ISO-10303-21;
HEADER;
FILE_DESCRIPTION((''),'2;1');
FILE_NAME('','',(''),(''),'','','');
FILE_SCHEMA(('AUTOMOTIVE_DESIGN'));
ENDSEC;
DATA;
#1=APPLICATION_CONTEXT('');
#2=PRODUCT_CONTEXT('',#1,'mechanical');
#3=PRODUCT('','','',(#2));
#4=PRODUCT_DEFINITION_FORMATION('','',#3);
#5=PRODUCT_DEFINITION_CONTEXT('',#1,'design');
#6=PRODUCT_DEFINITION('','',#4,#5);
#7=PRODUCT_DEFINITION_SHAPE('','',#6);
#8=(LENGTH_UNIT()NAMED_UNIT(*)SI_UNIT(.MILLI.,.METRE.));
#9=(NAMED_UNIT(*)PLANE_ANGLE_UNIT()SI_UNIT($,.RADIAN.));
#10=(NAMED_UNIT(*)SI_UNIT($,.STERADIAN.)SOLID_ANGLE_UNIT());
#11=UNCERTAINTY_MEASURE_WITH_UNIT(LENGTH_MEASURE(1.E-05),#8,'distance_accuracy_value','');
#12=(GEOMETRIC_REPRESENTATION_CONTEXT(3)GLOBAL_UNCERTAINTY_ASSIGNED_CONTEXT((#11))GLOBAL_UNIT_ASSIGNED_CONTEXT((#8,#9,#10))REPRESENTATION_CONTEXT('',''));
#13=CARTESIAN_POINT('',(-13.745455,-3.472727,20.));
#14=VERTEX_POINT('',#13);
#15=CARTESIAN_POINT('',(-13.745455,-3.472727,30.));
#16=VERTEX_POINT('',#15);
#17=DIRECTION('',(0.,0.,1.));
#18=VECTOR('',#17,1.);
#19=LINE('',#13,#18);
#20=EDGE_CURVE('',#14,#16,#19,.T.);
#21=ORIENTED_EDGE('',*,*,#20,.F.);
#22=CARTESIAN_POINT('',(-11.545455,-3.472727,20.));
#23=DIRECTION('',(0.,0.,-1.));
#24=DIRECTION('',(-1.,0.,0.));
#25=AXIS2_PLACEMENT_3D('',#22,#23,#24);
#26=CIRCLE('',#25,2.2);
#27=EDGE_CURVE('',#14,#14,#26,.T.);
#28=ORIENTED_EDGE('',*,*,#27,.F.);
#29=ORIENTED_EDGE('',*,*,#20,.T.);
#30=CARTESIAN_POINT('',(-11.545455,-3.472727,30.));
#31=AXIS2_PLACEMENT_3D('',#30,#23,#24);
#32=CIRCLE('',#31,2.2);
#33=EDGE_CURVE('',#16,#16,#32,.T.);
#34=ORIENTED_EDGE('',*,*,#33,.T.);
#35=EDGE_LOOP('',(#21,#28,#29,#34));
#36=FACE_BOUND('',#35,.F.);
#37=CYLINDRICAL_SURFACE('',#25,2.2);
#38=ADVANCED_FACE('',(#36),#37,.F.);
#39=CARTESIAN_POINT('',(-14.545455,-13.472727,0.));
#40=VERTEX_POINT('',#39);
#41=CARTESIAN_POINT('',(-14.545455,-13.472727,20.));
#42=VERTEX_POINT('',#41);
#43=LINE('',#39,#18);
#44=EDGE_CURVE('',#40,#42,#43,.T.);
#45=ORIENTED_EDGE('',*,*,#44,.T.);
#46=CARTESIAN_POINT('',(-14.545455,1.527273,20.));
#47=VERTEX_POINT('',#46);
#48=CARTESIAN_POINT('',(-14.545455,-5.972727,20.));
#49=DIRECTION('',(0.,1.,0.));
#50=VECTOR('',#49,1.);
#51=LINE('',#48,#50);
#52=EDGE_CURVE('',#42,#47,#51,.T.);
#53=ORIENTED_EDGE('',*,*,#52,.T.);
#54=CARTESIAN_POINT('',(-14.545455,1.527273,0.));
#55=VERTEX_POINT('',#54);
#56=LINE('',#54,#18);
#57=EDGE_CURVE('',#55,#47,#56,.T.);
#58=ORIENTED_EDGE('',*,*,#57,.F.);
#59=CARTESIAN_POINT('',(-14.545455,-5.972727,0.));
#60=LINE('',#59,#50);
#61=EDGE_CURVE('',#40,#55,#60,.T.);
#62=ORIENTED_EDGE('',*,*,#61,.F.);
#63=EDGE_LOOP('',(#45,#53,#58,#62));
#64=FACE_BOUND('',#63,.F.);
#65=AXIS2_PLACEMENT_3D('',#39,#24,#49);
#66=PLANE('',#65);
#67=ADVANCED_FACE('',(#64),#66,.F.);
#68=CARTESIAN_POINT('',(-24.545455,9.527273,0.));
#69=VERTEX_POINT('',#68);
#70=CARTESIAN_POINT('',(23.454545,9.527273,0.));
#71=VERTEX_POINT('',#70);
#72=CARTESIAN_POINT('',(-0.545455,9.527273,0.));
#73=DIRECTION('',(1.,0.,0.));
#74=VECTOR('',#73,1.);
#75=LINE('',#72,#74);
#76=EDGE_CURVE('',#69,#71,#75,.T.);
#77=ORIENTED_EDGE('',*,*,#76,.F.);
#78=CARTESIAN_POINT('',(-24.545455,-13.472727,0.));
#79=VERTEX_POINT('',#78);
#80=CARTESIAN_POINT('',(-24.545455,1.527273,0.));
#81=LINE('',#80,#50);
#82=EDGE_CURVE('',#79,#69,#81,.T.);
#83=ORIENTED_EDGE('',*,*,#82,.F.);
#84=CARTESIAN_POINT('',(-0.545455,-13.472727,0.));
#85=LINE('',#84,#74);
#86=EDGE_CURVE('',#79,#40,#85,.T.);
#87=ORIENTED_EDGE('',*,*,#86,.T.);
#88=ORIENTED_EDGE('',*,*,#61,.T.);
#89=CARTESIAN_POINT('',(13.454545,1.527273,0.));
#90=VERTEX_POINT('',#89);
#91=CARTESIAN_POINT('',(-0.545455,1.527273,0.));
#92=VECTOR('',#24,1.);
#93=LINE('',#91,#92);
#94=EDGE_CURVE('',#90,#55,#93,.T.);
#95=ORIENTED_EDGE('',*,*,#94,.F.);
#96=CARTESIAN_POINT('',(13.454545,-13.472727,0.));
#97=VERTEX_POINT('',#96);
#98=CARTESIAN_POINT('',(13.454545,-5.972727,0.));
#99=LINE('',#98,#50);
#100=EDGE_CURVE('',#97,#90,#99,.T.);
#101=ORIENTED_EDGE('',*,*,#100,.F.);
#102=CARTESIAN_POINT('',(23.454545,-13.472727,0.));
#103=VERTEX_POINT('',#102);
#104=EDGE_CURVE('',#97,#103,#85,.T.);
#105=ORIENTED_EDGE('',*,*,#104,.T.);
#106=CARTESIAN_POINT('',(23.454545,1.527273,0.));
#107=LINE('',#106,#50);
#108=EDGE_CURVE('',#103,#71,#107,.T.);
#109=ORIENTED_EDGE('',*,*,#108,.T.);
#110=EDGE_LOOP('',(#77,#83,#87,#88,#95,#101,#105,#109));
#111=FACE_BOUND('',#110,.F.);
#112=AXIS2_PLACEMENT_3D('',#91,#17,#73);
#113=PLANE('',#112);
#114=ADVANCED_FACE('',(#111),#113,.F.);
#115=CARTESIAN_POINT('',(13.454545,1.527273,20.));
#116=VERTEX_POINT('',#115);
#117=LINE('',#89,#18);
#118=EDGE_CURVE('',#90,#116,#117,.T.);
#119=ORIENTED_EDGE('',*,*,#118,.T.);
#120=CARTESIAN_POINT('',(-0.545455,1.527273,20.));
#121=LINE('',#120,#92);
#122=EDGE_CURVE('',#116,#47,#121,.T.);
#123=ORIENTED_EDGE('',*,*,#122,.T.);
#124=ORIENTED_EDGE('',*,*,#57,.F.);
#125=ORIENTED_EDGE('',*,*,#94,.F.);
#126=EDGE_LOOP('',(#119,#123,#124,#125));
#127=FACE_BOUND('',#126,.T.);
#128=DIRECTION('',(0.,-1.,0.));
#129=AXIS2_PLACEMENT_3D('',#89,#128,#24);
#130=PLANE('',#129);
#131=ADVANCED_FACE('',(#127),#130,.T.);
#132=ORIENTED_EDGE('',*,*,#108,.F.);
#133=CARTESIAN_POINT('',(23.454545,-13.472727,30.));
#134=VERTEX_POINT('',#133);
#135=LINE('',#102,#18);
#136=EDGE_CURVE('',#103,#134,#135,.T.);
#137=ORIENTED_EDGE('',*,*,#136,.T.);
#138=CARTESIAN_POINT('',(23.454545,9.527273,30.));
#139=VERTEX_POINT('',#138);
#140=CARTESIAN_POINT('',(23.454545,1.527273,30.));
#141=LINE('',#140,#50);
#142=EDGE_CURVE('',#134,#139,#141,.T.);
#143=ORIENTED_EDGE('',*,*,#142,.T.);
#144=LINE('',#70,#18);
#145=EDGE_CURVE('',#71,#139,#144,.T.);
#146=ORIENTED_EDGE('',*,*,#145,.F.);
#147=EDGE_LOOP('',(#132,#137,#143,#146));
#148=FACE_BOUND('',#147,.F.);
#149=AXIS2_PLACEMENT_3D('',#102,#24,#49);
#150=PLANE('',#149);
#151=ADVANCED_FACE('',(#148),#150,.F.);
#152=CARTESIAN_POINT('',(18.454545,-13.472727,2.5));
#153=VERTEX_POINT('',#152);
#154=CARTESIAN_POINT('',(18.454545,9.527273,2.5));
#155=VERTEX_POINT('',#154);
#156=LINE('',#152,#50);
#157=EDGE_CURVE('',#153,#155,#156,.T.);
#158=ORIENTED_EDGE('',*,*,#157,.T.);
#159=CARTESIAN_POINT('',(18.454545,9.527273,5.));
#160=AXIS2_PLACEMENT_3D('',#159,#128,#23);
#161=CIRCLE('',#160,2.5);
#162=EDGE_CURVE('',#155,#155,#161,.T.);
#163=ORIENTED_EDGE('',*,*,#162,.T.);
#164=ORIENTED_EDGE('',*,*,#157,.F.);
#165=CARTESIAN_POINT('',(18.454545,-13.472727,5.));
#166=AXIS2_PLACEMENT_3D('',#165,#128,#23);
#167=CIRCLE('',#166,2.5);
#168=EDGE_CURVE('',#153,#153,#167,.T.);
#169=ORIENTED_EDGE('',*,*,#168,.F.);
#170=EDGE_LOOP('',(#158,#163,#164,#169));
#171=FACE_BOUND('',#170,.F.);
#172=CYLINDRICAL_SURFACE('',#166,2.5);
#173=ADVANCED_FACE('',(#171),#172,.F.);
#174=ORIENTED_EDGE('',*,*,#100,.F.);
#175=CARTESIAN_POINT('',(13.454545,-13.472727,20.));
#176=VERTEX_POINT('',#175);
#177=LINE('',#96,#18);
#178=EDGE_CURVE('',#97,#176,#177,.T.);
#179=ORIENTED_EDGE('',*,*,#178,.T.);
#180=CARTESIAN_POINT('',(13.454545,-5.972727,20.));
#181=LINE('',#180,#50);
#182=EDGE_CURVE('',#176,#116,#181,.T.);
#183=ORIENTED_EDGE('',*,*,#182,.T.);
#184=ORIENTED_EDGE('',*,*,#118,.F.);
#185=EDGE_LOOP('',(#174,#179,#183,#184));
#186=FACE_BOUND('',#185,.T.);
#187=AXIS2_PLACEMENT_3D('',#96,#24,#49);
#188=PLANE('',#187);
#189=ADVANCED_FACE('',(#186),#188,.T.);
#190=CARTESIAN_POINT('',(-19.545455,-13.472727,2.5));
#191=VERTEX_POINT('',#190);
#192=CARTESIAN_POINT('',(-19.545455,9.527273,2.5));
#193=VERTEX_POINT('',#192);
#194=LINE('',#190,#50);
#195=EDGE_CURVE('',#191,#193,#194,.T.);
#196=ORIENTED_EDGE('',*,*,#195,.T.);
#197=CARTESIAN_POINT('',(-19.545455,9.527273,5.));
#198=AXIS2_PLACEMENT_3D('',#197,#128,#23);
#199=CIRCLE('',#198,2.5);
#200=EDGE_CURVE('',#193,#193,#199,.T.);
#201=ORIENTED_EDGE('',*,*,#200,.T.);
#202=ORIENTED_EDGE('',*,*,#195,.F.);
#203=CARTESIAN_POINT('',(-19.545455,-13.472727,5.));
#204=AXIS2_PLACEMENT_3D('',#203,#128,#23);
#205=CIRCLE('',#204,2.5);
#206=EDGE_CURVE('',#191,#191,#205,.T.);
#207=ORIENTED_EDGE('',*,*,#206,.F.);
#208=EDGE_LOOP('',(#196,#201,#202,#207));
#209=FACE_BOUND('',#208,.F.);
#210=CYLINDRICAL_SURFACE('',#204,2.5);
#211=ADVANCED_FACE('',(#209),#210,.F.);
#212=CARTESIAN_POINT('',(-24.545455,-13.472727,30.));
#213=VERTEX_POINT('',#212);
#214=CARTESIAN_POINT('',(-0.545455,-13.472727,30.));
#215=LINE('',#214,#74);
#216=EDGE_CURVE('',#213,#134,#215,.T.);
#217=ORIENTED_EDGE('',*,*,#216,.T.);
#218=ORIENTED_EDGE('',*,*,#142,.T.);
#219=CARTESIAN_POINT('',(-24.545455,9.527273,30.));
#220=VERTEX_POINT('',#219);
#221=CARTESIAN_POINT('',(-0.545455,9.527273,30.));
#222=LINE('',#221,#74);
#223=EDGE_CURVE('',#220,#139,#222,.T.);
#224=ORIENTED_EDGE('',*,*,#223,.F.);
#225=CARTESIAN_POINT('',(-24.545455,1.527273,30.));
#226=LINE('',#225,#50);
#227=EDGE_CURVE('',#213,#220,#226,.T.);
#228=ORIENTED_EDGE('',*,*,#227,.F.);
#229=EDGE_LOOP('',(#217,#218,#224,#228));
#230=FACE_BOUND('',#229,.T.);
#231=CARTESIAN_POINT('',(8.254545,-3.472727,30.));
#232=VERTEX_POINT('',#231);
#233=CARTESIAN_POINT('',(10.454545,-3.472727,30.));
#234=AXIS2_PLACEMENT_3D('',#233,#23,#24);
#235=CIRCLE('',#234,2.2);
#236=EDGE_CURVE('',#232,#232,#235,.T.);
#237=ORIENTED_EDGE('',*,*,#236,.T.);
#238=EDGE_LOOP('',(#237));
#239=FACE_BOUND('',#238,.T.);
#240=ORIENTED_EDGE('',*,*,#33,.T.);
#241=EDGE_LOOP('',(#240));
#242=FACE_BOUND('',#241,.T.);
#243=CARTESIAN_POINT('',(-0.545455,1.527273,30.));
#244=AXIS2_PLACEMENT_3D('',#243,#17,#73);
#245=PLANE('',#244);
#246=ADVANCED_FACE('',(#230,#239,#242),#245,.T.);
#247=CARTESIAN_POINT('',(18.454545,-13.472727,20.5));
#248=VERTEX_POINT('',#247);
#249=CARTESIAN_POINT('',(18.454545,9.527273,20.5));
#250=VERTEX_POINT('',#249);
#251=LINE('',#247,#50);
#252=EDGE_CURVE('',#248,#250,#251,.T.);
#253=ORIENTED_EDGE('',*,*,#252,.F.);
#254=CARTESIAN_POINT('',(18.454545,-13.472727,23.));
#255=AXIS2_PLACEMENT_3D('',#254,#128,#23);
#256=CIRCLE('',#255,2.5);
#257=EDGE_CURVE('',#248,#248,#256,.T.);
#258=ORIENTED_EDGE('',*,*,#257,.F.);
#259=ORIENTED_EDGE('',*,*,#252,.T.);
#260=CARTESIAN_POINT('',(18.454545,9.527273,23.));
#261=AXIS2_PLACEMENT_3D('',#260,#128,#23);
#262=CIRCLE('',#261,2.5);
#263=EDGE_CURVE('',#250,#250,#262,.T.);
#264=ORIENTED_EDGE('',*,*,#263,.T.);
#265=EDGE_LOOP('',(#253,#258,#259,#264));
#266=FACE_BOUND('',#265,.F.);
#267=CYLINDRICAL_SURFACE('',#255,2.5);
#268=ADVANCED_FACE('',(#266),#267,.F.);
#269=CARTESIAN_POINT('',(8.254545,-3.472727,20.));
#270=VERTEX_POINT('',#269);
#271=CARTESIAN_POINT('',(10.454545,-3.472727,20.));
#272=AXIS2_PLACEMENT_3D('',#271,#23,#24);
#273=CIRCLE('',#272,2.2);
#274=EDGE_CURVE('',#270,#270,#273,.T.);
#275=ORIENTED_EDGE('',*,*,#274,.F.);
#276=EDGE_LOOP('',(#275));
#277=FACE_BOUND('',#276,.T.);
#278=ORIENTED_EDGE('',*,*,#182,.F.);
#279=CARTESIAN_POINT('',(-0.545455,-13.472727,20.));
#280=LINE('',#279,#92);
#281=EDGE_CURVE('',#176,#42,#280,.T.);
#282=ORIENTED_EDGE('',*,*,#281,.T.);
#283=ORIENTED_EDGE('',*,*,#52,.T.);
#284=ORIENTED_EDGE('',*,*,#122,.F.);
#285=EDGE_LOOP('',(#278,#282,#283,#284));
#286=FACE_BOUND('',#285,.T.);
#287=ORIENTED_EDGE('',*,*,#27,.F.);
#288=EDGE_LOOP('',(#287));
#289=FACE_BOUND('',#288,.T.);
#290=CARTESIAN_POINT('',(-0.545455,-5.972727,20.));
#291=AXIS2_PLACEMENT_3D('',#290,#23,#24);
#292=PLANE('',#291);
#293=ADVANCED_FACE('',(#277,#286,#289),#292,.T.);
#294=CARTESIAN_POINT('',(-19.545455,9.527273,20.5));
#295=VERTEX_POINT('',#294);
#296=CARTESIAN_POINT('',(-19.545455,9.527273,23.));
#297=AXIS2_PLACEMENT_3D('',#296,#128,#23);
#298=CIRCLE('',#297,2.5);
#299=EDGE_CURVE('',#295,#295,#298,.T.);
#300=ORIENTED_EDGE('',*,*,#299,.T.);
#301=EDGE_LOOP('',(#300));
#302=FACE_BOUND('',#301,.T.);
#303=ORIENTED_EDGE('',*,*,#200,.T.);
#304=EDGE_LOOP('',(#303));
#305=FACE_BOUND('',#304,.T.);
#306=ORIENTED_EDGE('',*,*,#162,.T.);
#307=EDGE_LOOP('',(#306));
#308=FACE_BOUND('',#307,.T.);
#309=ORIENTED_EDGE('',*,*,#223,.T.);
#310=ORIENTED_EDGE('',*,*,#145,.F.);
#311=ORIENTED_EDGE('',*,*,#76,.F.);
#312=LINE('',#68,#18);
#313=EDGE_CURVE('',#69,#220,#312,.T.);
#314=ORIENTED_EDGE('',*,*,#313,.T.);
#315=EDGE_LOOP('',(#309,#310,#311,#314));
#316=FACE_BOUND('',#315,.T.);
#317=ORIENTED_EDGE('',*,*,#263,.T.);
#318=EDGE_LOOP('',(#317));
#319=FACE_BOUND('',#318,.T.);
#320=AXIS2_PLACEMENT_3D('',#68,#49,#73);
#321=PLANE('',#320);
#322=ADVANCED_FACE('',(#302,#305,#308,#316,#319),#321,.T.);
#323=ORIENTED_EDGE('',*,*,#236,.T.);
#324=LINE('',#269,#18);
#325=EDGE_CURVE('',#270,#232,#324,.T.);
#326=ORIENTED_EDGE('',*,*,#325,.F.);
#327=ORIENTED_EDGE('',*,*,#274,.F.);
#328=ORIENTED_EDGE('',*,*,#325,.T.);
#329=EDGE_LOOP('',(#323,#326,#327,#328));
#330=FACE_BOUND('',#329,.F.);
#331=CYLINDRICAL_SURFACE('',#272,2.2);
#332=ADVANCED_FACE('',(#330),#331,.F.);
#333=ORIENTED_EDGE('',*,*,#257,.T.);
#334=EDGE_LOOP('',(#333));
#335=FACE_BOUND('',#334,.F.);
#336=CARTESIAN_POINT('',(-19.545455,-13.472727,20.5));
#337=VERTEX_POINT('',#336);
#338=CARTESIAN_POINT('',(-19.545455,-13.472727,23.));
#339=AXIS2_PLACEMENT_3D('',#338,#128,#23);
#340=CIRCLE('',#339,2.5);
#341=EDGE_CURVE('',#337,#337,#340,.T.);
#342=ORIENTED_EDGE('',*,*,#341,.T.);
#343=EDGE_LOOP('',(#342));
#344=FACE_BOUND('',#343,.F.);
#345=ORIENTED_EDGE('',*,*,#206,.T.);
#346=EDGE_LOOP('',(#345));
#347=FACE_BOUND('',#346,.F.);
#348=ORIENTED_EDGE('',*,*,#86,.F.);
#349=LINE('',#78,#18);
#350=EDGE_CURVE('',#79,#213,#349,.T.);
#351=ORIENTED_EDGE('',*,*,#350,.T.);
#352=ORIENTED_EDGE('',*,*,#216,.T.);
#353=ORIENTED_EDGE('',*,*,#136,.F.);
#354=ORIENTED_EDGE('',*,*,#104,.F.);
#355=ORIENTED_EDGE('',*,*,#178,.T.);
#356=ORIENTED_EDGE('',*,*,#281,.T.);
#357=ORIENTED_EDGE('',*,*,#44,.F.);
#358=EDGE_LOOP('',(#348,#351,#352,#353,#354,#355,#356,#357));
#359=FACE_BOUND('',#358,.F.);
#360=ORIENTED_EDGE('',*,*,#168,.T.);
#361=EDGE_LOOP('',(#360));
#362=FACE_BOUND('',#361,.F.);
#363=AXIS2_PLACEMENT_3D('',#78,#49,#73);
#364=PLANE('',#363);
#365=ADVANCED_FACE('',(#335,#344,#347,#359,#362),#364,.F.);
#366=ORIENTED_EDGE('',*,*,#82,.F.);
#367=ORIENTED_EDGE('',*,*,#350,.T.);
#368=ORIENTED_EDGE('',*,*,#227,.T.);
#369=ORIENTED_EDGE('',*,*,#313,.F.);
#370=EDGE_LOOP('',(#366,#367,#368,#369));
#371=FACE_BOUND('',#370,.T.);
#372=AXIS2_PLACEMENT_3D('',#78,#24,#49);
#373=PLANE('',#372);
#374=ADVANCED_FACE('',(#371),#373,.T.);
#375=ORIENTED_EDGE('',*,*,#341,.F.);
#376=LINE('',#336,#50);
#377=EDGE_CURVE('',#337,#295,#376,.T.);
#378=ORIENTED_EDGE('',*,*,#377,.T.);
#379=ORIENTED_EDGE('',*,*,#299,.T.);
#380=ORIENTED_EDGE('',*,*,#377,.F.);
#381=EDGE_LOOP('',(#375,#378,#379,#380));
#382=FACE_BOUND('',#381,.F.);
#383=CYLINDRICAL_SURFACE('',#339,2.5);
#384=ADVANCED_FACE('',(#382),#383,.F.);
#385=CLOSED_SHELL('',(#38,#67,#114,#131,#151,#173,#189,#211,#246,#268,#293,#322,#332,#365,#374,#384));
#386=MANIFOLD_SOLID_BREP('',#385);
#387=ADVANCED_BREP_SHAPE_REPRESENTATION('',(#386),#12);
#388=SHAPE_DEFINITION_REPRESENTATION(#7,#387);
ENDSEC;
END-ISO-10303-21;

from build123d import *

# Parameters (mm, degrees)
SKETCH_1_W          = 48
SKETCH_1_H          = 30
EXTRUDE_1_DEPTH     = 30
SKETCH_2_W          = 28
SKETCH_2_H          = 15
CUT_EXTRUDE_1_DEPTH = 20
SKETCH_3_R          = 2.2
CUT_EXTRUDE_2_DEPTH = 20
SKETCH_4_R          = 2.5
CUT_EXTRUDE_3_DEPTH = 30
CUT_EXTRUDE_START   = -30
SKETCH_8_W          = 48
SKETCH_8_H          = 7
CUT_EXTRUDE_5_DEPTH = 30


with BuildPart() as part:
    # 草图1 → 凸台-拉伸1 (new body)
    with BuildSketch(Plane.XY):
        with Locations((-0.545454545, 1.527272727)):
            Rectangle(SKETCH_1_W, SKETCH_1_H)
    extrude(amount=EXTRUDE_1_DEPTH)

    # 草图2 → 切除-拉伸1 (cut)
    with BuildSketch(Plane(origin=(0, 0, 0), x_dir=(-1, 0, 0), z_dir=(0, 0, -1))):
        with Locations((0.545454545, -5.972727273)):
            Rectangle(SKETCH_2_W, SKETCH_2_H)
    extrude(amount=-CUT_EXTRUDE_1_DEPTH, mode=Mode.SUBTRACT)

    # 草图3 → 切除-拉伸2 (cut)
    with BuildSketch(Plane(origin=(0, 0, 20), x_dir=(-1, 0, 0), z_dir=(0, 0, -1))):
        with Locations((-10.454545455, -3.472727273)):
            Circle(SKETCH_3_R)
        with Locations((11.545454545, -3.472727273)):
            Circle(SKETCH_3_R)
    extrude(amount=-CUT_EXTRUDE_2_DEPTH, mode=Mode.SUBTRACT)

    # 草图4 → 切除-拉伸3 (cut)
    with BuildSketch(Plane.XZ.offset(13.472727273)):
        with Locations(Location((-19.545454545, 5, 0), (0, 0, 270))):
            Circle(SKETCH_4_R)
        with Locations(Location((-19.545454545, 23, 0), (0, 0, 270))):
            Circle(SKETCH_4_R)
        with Locations(Location((18.454545455, 23, 0), (0, 0, 270))):
            Circle(SKETCH_4_R)
        with Locations(Location((18.454545455, 5, 0), (0, 0, 270))):
            Circle(SKETCH_4_R)
    extrude(amount=-CUT_EXTRUDE_3_DEPTH, mode=Mode.SUBTRACT)

    # 草图8 → 切除-拉伸5 (cut)
    with BuildSketch(Plane.XY.offset(30).offset(CUT_EXTRUDE_START)):
        with Locations((-0.545454545, 13.027272727)):
            Rectangle(SKETCH_8_W, SKETCH_8_H)
    extrude(amount=CUT_EXTRUDE_5_DEPTH, mode=Mode.SUBTRACT)


solid = part.part
